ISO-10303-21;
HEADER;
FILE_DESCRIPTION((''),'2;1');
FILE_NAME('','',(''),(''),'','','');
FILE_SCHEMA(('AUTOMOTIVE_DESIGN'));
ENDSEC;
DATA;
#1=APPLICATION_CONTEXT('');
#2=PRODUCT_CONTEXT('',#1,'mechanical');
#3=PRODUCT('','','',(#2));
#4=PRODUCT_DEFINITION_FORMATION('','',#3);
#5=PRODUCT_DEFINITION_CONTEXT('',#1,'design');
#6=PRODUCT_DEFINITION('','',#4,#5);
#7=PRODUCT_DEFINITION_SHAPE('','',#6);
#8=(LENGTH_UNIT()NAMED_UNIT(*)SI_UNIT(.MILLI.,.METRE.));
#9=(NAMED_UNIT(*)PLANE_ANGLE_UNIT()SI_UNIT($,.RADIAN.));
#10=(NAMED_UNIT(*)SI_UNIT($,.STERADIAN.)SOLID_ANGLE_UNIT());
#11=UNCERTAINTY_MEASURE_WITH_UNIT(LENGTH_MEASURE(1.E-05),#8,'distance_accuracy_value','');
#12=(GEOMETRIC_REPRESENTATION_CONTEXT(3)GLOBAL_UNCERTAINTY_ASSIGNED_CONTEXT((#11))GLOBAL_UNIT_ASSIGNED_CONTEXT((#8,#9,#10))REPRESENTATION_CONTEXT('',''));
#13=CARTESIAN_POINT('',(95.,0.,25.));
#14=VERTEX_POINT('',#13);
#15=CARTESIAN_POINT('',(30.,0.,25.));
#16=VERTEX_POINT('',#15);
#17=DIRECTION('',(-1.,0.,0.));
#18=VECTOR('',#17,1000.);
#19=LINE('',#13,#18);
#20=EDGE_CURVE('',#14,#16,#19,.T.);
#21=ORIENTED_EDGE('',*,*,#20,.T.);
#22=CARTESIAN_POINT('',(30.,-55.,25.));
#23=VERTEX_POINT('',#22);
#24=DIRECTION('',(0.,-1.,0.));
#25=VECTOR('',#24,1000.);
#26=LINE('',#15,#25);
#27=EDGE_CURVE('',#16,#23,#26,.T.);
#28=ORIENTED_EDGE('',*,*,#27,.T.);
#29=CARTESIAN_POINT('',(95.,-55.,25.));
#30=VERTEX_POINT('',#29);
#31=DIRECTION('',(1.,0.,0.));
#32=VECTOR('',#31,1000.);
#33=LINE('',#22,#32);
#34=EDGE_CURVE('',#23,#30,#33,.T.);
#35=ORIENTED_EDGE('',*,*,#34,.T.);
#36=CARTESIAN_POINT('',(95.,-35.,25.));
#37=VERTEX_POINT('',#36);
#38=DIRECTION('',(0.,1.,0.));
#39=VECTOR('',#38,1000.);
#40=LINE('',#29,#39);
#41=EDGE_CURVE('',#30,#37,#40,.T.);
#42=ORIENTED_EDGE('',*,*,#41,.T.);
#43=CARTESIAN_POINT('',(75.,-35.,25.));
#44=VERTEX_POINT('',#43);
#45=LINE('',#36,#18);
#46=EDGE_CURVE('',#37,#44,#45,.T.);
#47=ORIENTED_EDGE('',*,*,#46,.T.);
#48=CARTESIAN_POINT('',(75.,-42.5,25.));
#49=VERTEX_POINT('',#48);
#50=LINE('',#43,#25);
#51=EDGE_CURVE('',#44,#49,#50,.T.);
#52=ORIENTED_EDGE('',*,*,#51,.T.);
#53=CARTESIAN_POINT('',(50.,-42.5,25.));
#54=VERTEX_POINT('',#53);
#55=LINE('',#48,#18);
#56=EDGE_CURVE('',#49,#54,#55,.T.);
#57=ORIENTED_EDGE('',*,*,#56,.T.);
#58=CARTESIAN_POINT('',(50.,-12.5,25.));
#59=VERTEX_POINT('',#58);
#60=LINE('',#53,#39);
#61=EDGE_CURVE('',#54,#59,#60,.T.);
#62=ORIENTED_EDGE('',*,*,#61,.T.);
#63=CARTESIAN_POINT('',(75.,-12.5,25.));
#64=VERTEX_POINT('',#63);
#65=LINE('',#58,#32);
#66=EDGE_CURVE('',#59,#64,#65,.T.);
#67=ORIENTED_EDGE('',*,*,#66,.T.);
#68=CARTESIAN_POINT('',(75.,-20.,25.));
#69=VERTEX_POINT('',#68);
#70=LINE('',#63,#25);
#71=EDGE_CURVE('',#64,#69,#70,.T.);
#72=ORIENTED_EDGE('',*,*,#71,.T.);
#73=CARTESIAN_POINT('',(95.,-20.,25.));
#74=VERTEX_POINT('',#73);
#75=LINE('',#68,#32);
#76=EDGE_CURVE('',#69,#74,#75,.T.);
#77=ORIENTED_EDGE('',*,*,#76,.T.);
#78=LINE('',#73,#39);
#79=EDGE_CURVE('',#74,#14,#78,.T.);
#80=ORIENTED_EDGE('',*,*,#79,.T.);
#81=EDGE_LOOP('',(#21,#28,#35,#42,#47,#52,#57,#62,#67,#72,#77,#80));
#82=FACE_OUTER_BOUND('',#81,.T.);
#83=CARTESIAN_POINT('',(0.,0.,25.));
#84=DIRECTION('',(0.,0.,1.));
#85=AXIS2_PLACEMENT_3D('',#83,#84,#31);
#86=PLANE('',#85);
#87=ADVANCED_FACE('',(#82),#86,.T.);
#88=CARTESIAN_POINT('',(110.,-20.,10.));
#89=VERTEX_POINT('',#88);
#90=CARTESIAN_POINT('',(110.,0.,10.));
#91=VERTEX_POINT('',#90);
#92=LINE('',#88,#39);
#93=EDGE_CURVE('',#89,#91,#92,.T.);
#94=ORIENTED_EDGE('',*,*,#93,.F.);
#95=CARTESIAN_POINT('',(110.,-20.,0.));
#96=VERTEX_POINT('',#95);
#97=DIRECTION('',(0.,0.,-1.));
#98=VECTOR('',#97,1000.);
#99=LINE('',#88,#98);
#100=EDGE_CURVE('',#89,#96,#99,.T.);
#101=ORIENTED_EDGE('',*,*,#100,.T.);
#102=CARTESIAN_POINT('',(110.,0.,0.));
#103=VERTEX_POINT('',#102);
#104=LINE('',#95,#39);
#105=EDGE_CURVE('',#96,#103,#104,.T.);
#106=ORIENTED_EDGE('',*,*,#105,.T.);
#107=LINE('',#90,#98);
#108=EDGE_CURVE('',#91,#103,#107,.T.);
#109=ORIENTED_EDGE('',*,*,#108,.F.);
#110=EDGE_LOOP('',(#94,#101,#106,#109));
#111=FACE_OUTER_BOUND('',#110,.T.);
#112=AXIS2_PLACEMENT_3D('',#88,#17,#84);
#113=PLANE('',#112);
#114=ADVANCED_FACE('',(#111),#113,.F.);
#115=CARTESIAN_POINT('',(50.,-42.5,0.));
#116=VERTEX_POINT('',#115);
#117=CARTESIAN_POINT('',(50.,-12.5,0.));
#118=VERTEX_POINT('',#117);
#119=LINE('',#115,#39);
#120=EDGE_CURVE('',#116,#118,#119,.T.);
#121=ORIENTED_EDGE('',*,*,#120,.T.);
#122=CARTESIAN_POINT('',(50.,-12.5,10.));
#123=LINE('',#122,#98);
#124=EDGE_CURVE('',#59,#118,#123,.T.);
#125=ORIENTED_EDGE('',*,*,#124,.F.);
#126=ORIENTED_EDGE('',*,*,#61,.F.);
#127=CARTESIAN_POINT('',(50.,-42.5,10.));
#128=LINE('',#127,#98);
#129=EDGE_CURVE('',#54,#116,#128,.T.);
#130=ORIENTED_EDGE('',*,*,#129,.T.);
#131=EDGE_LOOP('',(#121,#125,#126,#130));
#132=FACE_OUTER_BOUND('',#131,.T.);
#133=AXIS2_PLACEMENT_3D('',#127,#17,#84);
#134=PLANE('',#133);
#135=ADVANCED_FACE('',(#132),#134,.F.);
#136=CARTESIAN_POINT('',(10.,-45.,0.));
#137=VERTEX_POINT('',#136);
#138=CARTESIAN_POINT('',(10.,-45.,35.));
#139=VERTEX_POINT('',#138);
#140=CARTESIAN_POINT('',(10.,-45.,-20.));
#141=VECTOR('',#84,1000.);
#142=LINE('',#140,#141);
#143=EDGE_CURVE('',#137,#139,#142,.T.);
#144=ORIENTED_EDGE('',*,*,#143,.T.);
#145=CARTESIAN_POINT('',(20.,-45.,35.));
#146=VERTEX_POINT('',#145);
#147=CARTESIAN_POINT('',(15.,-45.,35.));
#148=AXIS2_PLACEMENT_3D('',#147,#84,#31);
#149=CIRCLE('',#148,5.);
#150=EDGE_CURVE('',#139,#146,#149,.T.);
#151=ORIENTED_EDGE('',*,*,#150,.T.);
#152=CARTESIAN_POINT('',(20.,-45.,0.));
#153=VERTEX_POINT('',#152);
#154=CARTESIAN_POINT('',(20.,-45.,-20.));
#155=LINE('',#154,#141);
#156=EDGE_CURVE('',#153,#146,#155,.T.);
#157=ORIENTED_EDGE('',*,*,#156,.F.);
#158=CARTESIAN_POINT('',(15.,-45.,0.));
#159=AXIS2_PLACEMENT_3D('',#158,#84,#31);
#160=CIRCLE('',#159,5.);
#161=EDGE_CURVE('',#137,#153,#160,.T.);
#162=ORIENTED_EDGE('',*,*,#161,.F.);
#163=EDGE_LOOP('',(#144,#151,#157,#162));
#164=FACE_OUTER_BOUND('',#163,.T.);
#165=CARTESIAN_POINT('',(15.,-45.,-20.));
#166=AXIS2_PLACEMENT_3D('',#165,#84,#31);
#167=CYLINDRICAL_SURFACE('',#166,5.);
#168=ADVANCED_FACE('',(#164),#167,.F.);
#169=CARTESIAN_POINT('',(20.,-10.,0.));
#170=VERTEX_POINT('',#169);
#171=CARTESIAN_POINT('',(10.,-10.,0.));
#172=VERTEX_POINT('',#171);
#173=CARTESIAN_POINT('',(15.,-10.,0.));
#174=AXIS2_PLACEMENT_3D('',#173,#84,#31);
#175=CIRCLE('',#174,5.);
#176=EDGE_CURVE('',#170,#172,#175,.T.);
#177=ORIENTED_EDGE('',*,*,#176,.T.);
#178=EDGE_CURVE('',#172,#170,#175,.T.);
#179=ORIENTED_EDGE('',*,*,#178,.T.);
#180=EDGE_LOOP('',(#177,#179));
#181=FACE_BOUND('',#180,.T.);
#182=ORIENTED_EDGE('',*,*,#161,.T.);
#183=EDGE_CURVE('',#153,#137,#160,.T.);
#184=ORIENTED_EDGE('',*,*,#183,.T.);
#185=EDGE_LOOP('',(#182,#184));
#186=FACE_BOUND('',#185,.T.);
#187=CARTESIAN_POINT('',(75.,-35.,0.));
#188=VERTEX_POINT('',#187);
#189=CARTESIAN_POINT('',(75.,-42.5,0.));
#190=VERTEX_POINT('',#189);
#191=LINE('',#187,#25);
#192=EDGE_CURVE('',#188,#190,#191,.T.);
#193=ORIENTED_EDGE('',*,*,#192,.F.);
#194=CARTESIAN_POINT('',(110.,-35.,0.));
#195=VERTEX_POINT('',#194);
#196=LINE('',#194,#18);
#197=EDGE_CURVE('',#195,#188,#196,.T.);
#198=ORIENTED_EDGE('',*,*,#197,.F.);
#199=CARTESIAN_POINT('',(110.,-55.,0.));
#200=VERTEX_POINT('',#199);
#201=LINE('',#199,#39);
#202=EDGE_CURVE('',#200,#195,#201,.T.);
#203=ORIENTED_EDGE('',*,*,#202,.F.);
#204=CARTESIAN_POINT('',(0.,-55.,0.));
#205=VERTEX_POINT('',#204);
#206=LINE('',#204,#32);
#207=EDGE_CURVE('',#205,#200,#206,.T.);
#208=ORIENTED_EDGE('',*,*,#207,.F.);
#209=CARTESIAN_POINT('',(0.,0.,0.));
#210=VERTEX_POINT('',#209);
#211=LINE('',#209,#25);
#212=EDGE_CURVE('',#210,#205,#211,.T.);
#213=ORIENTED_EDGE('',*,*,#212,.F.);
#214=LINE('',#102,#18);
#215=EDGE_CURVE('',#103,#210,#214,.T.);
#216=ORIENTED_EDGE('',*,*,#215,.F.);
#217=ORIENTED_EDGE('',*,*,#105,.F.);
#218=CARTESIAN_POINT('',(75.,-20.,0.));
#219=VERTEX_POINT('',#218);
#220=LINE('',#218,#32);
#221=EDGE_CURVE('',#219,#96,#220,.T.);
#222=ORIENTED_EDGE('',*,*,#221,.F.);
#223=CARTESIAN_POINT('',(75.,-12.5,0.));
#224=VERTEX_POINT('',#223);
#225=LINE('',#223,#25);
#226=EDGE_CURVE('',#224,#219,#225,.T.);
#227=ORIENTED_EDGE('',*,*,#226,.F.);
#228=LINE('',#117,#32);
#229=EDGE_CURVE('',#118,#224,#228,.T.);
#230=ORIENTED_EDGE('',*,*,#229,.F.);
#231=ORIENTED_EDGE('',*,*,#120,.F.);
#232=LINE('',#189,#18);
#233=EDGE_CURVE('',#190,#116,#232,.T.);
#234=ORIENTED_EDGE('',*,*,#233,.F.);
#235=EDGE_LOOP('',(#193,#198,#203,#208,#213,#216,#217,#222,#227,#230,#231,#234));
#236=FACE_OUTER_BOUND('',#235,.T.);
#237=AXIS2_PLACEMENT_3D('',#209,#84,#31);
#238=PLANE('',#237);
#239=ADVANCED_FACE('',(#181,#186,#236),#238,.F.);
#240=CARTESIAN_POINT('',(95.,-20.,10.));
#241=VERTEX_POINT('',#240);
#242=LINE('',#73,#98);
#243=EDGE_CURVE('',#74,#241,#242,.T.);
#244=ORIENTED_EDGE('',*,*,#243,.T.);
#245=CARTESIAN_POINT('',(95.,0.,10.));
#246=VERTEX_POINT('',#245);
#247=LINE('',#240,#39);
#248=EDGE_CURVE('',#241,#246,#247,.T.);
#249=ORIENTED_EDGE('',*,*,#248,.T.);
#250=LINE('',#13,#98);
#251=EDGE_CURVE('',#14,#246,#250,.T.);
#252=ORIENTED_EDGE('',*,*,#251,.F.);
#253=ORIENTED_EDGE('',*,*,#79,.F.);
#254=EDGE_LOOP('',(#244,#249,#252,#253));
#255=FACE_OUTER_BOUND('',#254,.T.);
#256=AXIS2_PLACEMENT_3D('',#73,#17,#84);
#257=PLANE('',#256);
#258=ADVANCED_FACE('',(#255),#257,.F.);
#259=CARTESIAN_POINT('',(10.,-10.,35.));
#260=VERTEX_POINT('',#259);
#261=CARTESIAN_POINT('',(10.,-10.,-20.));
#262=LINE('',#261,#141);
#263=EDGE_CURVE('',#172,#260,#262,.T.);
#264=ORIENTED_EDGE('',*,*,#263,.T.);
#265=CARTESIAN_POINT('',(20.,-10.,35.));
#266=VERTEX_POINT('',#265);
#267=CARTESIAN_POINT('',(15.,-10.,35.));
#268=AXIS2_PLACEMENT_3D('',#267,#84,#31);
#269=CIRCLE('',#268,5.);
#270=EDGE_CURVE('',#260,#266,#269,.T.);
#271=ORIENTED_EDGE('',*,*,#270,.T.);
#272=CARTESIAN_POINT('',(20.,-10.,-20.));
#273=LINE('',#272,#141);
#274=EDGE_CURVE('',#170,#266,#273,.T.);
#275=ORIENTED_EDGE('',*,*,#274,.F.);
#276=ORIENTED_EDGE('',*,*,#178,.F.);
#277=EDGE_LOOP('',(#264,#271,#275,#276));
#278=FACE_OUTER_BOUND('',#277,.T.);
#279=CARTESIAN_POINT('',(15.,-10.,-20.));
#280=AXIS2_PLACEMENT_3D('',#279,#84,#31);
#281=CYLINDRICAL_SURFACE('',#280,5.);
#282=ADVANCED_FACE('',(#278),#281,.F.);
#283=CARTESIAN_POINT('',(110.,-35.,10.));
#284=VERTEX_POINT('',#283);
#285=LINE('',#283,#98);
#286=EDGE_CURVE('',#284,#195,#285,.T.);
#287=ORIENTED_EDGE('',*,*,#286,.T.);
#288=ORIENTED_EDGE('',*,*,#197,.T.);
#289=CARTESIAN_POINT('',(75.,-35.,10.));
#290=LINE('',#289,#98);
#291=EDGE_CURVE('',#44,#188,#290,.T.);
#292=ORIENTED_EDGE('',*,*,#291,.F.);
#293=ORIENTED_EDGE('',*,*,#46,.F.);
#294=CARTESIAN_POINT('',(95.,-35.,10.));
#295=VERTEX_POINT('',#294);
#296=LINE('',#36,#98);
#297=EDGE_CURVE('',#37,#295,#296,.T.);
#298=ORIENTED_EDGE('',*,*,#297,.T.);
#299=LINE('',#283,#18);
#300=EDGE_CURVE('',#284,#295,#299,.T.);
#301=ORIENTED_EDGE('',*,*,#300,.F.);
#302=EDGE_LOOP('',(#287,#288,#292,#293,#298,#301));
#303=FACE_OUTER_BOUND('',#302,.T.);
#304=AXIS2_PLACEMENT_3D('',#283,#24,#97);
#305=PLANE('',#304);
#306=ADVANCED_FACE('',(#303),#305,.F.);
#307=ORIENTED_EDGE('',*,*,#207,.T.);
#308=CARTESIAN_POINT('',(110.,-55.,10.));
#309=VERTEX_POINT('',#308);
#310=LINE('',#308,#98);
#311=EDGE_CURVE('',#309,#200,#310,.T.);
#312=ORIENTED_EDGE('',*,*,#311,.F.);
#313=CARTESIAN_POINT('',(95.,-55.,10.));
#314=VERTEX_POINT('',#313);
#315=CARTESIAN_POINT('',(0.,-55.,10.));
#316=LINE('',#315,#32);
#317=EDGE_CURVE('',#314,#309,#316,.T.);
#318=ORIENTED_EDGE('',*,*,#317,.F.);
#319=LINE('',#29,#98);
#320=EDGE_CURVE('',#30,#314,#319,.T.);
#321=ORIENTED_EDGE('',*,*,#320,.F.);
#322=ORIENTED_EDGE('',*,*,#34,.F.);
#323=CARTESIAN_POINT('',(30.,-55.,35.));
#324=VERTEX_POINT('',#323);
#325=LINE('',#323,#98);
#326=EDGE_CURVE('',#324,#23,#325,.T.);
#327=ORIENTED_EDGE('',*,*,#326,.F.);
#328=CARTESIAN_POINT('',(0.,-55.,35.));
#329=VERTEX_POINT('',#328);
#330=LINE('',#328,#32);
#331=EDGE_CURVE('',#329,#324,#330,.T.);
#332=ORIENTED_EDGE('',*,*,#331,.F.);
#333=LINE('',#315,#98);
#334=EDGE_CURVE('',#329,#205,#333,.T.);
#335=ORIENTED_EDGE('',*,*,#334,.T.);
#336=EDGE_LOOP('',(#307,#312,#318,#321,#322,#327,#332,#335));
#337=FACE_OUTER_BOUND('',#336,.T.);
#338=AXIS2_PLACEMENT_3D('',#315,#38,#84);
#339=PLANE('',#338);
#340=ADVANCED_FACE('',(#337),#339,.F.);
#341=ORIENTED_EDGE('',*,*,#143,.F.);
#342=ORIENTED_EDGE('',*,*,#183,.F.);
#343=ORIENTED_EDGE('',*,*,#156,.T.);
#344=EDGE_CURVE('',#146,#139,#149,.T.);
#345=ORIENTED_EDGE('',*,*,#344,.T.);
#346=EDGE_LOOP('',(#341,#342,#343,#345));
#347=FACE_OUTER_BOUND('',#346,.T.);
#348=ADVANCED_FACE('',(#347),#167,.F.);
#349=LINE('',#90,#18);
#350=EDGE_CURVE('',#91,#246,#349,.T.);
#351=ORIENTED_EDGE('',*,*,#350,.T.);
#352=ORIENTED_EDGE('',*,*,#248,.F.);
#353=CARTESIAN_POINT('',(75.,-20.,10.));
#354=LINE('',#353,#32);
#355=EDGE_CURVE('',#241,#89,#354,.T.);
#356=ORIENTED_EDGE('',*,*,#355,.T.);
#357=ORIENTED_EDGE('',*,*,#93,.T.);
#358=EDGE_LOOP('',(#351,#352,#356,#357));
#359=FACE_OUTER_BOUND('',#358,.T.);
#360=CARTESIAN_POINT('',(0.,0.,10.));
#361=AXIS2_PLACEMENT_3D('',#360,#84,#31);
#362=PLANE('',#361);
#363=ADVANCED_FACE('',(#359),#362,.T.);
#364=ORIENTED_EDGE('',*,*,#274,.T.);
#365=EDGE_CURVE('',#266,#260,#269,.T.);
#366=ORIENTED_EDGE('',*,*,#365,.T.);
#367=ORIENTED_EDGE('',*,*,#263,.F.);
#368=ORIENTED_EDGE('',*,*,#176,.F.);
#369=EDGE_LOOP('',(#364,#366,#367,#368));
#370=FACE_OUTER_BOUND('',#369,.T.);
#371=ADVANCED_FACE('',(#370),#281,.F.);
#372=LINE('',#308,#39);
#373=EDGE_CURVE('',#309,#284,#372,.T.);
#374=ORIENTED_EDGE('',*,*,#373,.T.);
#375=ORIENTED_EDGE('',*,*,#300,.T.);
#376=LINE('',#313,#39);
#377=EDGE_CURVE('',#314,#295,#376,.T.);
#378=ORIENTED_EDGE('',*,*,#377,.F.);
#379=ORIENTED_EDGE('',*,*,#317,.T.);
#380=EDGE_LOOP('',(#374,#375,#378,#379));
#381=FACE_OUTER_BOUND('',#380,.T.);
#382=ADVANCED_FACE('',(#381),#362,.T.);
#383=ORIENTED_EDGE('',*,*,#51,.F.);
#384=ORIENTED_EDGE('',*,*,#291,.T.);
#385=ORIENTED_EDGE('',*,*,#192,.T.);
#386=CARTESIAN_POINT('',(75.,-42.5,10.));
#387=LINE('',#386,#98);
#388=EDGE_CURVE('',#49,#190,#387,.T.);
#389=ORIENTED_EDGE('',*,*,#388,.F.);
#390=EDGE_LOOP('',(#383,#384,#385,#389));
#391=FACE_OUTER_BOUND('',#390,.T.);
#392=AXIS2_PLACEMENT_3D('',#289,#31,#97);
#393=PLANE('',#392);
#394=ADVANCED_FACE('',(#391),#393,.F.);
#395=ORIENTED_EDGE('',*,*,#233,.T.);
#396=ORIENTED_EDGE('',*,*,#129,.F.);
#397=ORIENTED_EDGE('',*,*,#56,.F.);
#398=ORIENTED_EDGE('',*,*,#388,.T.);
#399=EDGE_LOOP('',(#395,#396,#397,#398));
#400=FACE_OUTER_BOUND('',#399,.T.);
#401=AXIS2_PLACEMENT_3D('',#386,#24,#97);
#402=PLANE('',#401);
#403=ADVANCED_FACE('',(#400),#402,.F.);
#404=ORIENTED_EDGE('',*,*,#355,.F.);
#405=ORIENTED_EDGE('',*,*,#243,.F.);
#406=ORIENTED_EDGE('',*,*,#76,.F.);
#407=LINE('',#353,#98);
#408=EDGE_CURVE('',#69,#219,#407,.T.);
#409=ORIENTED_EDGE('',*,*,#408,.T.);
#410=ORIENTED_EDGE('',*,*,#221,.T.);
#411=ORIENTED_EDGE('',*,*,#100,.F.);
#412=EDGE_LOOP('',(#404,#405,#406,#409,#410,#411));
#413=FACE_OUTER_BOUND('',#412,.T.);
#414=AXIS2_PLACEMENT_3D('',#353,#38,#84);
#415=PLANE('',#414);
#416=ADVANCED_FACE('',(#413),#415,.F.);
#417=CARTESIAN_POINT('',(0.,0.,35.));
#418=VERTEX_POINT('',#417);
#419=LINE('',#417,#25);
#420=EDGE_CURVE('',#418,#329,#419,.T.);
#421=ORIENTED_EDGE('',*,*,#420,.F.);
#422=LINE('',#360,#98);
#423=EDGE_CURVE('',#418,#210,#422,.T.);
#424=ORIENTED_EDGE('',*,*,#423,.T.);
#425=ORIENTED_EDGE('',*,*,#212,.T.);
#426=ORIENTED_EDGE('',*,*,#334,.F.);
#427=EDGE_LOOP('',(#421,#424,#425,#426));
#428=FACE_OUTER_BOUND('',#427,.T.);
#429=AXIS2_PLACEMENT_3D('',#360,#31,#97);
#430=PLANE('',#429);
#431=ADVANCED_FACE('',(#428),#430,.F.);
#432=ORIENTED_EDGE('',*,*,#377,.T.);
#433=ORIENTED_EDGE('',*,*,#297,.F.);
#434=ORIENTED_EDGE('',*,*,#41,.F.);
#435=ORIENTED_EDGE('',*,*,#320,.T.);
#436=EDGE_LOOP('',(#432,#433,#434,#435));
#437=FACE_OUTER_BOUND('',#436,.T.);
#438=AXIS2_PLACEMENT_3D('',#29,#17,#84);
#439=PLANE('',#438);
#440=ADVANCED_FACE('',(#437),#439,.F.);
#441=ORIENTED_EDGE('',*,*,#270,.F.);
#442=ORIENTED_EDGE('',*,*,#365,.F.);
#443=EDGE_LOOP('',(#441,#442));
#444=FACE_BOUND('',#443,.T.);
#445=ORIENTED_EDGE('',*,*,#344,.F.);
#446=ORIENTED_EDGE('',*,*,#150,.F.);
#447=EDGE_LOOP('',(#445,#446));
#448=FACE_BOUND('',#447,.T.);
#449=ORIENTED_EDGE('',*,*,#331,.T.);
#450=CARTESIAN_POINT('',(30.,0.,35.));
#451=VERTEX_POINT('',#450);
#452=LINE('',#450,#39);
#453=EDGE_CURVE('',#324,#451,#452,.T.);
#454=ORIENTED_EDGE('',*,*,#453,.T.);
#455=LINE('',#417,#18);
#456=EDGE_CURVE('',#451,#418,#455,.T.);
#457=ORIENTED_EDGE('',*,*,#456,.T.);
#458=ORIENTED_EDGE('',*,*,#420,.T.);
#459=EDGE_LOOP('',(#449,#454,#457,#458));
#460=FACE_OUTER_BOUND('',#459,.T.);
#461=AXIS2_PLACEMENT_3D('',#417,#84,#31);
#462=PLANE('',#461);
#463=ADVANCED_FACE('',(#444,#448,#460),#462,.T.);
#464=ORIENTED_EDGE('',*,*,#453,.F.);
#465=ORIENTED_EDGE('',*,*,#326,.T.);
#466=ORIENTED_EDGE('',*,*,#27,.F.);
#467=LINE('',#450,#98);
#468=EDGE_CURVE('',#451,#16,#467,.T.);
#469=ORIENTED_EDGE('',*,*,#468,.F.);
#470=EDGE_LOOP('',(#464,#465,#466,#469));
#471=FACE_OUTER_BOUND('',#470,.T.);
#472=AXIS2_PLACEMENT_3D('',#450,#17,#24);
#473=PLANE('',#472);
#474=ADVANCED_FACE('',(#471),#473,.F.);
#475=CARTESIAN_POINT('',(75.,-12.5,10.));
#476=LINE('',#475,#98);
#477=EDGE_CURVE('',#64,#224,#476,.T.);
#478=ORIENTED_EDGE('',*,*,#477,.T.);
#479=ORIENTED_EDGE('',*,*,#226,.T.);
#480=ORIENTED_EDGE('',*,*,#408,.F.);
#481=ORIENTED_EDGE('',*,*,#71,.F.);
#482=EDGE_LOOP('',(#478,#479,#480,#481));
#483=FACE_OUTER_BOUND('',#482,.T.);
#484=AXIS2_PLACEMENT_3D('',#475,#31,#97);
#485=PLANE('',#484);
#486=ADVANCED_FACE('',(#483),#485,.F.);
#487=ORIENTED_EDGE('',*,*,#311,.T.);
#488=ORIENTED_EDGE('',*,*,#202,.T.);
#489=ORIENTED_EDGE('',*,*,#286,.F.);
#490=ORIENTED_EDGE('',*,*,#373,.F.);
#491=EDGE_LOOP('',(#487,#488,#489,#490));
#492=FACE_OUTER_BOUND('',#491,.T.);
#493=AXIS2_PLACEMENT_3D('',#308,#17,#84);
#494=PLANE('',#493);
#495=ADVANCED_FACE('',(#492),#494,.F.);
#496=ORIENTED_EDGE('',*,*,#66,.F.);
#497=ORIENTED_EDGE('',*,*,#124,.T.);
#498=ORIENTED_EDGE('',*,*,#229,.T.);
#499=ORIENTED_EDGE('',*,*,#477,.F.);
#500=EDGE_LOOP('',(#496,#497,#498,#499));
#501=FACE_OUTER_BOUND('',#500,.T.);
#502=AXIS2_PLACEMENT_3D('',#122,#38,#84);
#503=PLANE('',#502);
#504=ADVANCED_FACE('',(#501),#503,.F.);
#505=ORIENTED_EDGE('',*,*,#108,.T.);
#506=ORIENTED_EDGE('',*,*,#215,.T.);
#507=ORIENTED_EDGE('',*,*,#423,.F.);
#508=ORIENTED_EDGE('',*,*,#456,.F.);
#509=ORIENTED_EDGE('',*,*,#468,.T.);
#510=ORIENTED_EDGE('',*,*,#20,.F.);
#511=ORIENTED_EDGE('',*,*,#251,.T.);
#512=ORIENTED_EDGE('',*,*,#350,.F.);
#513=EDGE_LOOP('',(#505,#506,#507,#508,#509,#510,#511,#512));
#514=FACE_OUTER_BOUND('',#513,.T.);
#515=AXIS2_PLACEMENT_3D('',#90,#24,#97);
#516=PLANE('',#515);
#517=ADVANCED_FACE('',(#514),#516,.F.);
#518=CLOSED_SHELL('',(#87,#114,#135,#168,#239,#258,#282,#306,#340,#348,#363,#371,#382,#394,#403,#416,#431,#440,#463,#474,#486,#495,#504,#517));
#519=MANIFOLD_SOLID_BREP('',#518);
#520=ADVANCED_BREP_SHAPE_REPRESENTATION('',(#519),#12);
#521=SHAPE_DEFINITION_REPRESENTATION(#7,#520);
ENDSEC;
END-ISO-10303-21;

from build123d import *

# Parameters (mm, degrees)
BASE_PROFILE_DEPTH     = 10
UPRIGHT_BLOCK_SKETCH_W = 30
UPRIGHT_BLOCK_SKETCH_H = 55
UPRIGHT_BLOCK_DEPTH    = 25
SLOTTED_ARM_DEPTH      = 15
THROUGH_HOLES_SKETCH_R = 5
THROUGH_HOLES_2X_DEPTH = 55


with BuildPart() as part:
    # Base Profile Sketch → Base Profile (new body)
    with BuildSketch(Plane.XY):
        Polygon((0, 0), (0, -55), (110, -55), (110, -35), (75, -35), (75, -42.5), (50, -42.5), (50, -12.5), (75, -12.5), (75, -20), (110, -20), (110, 0), align=None)
    extrude(amount=BASE_PROFILE_DEPTH)

    # Upright Block Sketch → Upright Block (add)
    with BuildSketch(Plane.XY.offset(10)):
        with Locations((15, -27.5)):
            Rectangle(UPRIGHT_BLOCK_SKETCH_W, UPRIGHT_BLOCK_SKETCH_H)
    extrude(amount=UPRIGHT_BLOCK_DEPTH)

    # Slotted Arm Sketch → Slotted Arm (add)
    with BuildSketch(Plane.XY.offset(10)):
        Polygon((30, 0), (30, -55), (95, -55), (95, -35), (75, -35), (75, -42.5), (50, -42.5), (50, -12.5), (75, -12.5), (75, -20), (95, -20), (95, 0), align=None)
    extrude(amount=SLOTTED_ARM_DEPTH)

    # Through Holes Sketch → Through Holes 2x (cut)
    with BuildSketch(Plane.XY.offset(35)):
        with Locations((15, -10)):
            Circle(THROUGH_HOLES_SKETCH_R)
        with Locations((15, -45)):
            Circle(THROUGH_HOLES_SKETCH_R)
    extrude(amount=-THROUGH_HOLES_2X_DEPTH, mode=Mode.SUBTRACT)


solid = part.part
